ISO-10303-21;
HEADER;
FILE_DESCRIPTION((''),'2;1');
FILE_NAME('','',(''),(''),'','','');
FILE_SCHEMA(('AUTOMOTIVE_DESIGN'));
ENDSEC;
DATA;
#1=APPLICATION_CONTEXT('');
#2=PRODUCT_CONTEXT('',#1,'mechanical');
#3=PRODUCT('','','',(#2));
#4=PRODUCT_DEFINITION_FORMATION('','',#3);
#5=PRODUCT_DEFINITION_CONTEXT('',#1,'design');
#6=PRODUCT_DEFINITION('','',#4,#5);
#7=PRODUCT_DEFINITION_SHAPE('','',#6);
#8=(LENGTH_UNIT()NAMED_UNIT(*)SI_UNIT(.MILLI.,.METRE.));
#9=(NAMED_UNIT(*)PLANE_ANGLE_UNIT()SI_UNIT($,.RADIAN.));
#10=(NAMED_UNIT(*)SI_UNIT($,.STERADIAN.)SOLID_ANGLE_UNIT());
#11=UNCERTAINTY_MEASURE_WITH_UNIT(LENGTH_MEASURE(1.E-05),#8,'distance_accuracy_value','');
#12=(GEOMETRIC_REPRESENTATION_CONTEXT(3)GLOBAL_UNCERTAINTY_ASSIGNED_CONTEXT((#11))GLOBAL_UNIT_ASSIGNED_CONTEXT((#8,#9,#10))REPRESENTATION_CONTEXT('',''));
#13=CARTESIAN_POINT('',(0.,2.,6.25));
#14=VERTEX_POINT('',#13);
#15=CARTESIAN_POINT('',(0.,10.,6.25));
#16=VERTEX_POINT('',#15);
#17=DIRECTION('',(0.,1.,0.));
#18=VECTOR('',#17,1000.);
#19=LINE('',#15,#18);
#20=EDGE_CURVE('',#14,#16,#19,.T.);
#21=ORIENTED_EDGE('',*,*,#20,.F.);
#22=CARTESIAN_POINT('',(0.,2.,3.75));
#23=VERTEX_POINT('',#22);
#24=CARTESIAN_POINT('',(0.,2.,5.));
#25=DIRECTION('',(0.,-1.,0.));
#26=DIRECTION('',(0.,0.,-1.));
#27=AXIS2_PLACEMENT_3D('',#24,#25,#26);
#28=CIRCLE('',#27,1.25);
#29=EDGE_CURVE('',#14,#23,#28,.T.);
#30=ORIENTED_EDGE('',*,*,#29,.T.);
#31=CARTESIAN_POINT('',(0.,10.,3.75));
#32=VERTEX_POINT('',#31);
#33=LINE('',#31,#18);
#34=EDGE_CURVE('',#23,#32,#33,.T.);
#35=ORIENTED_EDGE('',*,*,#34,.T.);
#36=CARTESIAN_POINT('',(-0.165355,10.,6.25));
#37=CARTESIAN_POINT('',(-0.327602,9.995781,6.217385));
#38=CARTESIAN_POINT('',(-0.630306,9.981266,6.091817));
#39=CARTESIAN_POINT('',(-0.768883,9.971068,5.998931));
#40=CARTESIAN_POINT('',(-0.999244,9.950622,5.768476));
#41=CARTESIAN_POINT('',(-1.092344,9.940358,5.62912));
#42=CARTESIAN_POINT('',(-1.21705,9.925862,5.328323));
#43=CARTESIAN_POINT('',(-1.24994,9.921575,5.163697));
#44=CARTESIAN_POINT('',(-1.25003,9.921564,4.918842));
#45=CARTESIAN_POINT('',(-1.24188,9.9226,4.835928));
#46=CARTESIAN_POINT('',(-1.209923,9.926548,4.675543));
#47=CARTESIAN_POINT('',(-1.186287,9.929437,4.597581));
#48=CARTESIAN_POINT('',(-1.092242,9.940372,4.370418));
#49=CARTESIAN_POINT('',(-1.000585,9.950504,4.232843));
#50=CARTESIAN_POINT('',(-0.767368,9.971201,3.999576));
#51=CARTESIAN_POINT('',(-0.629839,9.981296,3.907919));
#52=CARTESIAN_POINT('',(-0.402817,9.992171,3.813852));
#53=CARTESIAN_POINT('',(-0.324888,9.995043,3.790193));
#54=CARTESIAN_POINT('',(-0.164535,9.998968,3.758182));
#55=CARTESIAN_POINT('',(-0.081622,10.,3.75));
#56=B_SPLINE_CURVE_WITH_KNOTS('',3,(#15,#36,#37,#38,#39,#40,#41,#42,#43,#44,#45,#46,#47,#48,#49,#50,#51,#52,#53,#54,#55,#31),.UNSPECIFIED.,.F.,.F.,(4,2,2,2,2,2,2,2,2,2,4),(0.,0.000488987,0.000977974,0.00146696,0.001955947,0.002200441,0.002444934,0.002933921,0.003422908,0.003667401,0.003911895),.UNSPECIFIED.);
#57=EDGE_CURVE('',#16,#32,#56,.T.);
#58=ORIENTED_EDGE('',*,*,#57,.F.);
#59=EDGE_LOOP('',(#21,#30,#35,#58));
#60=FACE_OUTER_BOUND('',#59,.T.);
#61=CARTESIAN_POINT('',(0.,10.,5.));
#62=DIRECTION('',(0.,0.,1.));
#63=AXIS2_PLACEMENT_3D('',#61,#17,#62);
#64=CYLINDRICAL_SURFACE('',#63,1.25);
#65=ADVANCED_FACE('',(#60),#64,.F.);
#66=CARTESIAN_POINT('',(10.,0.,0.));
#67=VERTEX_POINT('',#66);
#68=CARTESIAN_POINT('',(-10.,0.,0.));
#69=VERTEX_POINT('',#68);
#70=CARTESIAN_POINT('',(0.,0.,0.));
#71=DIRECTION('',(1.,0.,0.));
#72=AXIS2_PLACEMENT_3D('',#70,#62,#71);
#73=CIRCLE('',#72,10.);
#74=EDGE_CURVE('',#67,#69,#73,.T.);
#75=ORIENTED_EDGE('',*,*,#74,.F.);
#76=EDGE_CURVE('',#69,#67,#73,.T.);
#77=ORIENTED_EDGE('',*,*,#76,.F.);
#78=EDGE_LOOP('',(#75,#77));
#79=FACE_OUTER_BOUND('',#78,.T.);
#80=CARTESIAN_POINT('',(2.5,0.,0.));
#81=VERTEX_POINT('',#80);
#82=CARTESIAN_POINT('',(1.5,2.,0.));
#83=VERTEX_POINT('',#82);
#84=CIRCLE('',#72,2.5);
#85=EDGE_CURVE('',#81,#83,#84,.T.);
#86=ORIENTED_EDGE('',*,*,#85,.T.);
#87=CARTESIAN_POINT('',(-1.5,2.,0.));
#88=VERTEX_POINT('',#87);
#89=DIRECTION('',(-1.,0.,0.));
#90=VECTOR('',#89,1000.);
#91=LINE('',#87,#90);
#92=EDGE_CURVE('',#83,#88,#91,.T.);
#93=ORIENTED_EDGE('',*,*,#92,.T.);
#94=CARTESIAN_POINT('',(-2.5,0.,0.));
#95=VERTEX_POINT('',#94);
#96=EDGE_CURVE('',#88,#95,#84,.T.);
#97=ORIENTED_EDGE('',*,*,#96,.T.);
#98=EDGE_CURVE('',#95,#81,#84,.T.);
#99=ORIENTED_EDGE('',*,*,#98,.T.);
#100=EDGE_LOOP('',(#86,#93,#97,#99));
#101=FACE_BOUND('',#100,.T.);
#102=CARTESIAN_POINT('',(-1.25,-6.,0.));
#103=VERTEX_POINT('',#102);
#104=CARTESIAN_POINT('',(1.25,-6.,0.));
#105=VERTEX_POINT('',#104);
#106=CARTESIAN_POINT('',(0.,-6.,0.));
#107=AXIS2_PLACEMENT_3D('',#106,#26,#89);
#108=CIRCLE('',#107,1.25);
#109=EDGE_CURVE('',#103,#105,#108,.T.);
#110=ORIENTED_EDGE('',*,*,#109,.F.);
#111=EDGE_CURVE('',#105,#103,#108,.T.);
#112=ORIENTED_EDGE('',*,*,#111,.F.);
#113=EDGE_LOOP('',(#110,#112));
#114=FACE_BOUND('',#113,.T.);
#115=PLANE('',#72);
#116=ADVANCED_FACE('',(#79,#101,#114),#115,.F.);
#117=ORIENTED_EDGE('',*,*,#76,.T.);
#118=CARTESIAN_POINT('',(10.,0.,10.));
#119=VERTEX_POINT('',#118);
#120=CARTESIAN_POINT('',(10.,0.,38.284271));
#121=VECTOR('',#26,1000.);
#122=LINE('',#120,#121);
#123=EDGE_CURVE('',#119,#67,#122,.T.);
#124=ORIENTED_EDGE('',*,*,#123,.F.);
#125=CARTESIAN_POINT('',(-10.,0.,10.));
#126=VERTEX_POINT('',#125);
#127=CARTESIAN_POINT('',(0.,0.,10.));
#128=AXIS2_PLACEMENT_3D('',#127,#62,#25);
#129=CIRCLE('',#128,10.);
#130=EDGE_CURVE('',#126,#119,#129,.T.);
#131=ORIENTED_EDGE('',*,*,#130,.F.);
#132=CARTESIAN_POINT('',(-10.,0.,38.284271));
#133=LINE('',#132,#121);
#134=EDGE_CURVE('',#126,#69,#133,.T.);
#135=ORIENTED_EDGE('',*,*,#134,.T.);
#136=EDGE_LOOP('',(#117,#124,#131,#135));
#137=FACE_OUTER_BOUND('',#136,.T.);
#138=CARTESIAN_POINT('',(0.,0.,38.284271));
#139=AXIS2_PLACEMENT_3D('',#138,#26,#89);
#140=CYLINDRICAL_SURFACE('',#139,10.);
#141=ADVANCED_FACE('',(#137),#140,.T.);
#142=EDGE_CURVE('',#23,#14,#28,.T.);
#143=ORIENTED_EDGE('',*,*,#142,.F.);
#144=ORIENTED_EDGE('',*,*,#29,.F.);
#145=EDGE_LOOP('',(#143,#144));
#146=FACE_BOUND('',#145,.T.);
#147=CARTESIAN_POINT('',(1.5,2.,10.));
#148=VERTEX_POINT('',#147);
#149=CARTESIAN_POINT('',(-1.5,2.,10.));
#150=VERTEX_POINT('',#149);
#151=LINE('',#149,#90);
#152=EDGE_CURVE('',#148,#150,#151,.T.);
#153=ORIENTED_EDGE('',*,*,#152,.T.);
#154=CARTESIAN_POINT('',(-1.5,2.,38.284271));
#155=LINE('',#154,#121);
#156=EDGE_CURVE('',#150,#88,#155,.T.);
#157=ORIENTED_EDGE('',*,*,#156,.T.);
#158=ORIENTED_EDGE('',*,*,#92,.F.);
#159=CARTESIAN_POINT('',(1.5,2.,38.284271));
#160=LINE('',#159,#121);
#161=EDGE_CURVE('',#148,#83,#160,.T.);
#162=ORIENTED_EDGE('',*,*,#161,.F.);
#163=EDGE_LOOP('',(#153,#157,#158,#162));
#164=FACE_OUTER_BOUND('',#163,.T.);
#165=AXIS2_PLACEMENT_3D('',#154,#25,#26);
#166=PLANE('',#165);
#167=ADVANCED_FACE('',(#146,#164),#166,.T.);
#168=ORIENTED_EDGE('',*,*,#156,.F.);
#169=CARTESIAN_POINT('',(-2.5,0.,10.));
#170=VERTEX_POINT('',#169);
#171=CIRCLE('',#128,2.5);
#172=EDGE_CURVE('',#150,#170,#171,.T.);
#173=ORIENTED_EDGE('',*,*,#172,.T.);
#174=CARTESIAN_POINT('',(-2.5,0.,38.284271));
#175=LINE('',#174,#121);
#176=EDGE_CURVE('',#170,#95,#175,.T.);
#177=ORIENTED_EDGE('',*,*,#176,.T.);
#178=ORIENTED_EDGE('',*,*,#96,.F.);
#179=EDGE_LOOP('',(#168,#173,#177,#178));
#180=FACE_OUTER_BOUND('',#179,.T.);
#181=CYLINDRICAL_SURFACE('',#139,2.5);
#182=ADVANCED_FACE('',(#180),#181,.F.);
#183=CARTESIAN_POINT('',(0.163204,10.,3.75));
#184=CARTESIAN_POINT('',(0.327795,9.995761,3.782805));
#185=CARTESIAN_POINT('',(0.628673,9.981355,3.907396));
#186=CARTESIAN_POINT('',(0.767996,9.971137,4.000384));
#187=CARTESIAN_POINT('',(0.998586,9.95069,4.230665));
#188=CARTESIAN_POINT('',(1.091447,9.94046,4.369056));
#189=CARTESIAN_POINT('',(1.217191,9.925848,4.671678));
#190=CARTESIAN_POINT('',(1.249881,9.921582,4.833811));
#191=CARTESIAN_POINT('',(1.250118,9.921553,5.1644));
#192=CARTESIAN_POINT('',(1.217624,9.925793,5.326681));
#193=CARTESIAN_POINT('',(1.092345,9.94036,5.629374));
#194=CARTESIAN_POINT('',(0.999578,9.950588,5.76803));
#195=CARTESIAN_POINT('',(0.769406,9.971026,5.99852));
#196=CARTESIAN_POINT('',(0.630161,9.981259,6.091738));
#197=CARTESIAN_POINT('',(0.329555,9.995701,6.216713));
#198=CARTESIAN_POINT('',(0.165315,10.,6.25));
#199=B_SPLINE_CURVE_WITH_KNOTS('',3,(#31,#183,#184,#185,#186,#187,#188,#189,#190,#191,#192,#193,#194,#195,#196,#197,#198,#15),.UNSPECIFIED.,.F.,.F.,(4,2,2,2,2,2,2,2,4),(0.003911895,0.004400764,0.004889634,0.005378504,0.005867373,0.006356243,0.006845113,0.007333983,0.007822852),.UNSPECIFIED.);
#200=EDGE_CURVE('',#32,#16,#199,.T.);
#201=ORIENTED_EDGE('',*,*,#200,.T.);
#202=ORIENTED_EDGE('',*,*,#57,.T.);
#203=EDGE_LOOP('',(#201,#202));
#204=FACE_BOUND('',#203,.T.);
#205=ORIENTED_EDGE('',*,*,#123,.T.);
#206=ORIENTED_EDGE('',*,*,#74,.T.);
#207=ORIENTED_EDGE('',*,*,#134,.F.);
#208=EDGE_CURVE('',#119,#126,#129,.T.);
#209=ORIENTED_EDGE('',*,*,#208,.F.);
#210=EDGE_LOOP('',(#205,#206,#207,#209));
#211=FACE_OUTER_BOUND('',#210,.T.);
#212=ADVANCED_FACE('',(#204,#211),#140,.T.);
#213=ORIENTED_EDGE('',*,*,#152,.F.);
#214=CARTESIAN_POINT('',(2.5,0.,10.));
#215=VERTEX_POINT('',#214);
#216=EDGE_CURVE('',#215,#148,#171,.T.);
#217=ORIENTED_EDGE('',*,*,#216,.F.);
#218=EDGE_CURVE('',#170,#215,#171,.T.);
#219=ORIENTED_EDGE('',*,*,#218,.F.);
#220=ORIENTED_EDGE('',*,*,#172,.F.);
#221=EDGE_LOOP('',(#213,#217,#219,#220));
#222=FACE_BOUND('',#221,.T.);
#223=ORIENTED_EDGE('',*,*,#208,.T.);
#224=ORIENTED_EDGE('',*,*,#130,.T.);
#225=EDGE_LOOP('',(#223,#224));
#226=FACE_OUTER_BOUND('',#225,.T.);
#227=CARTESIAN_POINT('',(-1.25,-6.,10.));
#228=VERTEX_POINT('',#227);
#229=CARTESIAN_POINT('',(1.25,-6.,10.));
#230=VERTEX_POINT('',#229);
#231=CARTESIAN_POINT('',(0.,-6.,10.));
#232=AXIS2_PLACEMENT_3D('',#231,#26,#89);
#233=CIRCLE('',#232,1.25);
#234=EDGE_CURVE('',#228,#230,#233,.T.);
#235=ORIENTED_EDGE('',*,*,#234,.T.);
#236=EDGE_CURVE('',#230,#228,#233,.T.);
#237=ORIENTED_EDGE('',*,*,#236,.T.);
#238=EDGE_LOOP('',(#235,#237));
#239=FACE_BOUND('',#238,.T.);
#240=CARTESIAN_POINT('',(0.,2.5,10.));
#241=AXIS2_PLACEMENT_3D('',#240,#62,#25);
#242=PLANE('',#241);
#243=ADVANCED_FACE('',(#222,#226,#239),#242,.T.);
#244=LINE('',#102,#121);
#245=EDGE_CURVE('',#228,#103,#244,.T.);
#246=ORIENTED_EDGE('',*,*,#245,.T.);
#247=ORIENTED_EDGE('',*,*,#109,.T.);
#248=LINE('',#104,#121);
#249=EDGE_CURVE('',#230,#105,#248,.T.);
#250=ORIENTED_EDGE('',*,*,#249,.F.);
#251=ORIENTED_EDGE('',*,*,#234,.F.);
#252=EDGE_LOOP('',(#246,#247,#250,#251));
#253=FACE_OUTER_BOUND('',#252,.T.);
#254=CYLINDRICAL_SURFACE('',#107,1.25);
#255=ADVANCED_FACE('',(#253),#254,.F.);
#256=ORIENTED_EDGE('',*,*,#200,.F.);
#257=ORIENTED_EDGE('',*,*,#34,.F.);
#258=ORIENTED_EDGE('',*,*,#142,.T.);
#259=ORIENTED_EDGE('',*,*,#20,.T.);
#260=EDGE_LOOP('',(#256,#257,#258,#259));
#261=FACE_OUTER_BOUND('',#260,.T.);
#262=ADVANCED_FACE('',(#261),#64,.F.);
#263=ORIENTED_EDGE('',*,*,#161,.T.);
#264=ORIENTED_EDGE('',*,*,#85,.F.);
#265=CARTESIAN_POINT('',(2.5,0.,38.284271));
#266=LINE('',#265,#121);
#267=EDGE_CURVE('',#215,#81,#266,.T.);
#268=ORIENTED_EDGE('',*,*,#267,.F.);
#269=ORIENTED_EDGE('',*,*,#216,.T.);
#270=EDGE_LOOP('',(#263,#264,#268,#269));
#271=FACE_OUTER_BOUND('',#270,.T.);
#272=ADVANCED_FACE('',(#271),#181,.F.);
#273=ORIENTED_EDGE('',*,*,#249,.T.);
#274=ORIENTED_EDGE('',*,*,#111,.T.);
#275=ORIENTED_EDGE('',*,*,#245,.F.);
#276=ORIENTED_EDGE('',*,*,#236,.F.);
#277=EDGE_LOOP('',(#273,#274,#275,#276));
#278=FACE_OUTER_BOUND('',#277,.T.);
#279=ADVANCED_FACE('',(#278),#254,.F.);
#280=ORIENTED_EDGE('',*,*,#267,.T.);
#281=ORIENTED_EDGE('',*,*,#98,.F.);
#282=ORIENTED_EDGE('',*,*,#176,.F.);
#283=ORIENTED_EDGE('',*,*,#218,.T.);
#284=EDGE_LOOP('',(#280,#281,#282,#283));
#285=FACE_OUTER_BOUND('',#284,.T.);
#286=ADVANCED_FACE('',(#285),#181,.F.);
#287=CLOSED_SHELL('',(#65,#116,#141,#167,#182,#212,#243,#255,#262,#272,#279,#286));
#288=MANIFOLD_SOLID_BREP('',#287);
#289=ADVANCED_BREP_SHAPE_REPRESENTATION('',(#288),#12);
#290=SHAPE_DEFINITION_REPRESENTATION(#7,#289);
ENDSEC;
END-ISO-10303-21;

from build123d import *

# Parameters (mm, degrees)
SKETCH_1_R             = 10
EXTRUDE_1_DEPTH        = 10
SKETCH_2_R             = 0.5
CUT_EXTRUDE_1_DEPTH    = 18.320508076
HOLE_WIZARD_M3_1_D     = 2.5
HOLE_WIZARD_M3_1_DEPTH = 8
HOLE_WIZARD_M3_2_D     = 2.5


with BuildPart() as part:
    # 草图1 → 凸台-拉伸1 (new body)
    with BuildSketch(Plane.XY):
        with Locations(Location((0, 0, 0), (0, 0, 270))):
            Circle(SKETCH_1_R)
        with BuildLine():
            Line((-1.5, 2), (1.5, 2))
            ThreePointArc((1.5, 2), (0, -2.5), (-1.5, 2))
        make_face(mode=Mode.SUBTRACT)
    extrude(amount=EXTRUDE_1_DEPTH)

    # 草图2 → 切除-拉伸1 (cut, through all)
    with BuildSketch(Plane.XY.offset(10)):
        with Locations((0, -6)):
            Circle(SKETCH_2_R)
    extrude(amount=-CUT_EXTRUDE_1_DEPTH, mode=Mode.SUBTRACT)

    # M3 螺纹孔1
    with Locations(Plane(origin=(234.411749502, 10, 915.569975215), x_dir=(-1, 0, 0), z_dir=(0, 1, 0))):
        with Locations((234.411749502, -910.569975215)):
            Hole(HOLE_WIZARD_M3_1_D / 2, depth=HOLE_WIZARD_M3_1_DEPTH)

    # M3 螺纹孔2 (through all)
    with Locations(Plane(origin=(0, 0, 0), x_dir=(-1, 0, 0), z_dir=(0, 0, -1))):
        with Locations((0, -6)):
            Hole(HOLE_WIZARD_M3_2_D / 2)


solid = part.part
